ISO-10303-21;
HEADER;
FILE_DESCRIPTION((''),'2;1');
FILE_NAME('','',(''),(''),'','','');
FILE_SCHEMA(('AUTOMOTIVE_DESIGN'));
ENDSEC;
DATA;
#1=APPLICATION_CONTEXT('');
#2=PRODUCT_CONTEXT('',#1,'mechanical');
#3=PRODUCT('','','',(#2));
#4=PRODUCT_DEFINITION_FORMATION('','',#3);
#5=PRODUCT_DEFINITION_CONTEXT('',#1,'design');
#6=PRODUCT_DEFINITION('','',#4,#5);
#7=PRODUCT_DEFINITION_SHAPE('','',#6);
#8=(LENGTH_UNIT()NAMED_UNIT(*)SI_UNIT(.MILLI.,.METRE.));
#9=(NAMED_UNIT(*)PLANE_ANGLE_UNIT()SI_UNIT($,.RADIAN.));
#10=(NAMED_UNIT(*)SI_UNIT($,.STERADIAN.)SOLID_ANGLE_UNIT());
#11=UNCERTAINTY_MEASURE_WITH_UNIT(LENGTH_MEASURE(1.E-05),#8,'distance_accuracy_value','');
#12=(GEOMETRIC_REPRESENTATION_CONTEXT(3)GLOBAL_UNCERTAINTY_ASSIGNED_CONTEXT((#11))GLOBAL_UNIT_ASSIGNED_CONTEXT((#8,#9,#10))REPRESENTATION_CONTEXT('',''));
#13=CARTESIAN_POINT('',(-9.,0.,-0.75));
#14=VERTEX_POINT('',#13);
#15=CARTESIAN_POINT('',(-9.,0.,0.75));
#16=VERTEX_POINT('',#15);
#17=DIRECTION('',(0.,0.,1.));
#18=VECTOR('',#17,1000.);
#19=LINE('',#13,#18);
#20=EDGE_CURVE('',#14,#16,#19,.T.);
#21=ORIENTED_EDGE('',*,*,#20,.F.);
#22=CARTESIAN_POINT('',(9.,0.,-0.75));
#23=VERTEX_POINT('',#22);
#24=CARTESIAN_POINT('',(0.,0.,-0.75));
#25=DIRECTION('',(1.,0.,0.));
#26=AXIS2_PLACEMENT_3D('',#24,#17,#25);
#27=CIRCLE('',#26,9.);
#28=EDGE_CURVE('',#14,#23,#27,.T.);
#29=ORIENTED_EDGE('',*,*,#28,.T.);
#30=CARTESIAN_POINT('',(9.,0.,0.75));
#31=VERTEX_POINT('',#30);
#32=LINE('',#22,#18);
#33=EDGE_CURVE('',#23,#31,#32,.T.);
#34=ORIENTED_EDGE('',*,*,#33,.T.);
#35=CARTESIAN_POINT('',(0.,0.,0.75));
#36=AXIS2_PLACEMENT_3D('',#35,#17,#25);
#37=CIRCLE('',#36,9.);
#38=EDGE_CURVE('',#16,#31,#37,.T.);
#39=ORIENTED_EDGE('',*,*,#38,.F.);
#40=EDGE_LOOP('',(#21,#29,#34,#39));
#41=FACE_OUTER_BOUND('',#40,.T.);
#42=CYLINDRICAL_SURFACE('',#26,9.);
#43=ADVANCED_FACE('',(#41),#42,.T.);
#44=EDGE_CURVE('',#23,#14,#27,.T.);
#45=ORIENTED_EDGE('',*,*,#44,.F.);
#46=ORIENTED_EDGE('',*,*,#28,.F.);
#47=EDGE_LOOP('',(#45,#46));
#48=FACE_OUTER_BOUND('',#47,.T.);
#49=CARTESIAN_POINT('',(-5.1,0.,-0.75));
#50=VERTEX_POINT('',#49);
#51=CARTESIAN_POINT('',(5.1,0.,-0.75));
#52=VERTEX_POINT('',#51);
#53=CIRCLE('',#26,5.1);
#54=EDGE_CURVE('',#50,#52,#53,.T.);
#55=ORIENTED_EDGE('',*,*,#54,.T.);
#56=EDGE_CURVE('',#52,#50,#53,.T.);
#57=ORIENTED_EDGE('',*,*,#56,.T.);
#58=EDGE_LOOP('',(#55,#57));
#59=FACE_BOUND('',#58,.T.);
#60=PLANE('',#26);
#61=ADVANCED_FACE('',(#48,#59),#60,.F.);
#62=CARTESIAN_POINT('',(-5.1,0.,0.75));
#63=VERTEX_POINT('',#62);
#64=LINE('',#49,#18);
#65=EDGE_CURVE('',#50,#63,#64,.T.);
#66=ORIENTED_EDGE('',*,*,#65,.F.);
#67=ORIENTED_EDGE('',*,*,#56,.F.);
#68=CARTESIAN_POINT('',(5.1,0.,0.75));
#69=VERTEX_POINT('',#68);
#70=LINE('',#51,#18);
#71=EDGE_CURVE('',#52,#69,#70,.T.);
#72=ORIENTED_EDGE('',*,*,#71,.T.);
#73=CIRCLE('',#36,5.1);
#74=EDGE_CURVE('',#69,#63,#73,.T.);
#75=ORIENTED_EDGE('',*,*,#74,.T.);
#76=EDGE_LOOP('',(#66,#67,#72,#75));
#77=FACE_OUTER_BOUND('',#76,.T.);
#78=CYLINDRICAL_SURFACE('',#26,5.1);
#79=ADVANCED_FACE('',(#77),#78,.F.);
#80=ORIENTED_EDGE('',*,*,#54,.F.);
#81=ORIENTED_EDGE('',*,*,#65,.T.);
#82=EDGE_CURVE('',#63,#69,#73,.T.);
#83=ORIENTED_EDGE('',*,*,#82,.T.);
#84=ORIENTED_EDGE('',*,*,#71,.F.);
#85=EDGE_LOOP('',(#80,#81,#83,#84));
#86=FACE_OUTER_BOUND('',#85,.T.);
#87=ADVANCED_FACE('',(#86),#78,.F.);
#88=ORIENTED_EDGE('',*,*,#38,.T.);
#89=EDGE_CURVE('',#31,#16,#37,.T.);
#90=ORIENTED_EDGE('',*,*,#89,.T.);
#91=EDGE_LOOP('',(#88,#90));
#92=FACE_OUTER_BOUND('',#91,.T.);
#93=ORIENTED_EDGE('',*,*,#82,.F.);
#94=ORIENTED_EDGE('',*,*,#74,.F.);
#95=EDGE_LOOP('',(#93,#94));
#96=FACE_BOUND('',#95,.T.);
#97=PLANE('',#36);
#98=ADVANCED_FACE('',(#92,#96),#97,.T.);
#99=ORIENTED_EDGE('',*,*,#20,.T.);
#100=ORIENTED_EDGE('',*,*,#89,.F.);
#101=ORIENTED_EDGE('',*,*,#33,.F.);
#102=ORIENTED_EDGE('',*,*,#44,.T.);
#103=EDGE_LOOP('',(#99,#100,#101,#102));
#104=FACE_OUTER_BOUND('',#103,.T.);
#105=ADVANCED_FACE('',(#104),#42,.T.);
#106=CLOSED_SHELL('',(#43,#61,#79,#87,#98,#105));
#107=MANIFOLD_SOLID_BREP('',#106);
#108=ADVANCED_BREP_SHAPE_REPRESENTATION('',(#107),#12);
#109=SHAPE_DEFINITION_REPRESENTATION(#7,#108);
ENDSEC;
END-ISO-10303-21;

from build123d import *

# Parameters (mm, degrees)
SKETCH_1_R      = 9
SKETCH_1_R_2    = 5.1
EXTRUDE_1_DEPTH = 0.75


with BuildPart() as part:
    # 草图1 → 凸台-拉伸1 (new, symmetric)
    with BuildSketch(Plane.XY):
        Circle(SKETCH_1_R)
        Circle(SKETCH_1_R_2, mode=Mode.SUBTRACT)
    extrude(amount=EXTRUDE_1_DEPTH, both=True)


solid = part.part
